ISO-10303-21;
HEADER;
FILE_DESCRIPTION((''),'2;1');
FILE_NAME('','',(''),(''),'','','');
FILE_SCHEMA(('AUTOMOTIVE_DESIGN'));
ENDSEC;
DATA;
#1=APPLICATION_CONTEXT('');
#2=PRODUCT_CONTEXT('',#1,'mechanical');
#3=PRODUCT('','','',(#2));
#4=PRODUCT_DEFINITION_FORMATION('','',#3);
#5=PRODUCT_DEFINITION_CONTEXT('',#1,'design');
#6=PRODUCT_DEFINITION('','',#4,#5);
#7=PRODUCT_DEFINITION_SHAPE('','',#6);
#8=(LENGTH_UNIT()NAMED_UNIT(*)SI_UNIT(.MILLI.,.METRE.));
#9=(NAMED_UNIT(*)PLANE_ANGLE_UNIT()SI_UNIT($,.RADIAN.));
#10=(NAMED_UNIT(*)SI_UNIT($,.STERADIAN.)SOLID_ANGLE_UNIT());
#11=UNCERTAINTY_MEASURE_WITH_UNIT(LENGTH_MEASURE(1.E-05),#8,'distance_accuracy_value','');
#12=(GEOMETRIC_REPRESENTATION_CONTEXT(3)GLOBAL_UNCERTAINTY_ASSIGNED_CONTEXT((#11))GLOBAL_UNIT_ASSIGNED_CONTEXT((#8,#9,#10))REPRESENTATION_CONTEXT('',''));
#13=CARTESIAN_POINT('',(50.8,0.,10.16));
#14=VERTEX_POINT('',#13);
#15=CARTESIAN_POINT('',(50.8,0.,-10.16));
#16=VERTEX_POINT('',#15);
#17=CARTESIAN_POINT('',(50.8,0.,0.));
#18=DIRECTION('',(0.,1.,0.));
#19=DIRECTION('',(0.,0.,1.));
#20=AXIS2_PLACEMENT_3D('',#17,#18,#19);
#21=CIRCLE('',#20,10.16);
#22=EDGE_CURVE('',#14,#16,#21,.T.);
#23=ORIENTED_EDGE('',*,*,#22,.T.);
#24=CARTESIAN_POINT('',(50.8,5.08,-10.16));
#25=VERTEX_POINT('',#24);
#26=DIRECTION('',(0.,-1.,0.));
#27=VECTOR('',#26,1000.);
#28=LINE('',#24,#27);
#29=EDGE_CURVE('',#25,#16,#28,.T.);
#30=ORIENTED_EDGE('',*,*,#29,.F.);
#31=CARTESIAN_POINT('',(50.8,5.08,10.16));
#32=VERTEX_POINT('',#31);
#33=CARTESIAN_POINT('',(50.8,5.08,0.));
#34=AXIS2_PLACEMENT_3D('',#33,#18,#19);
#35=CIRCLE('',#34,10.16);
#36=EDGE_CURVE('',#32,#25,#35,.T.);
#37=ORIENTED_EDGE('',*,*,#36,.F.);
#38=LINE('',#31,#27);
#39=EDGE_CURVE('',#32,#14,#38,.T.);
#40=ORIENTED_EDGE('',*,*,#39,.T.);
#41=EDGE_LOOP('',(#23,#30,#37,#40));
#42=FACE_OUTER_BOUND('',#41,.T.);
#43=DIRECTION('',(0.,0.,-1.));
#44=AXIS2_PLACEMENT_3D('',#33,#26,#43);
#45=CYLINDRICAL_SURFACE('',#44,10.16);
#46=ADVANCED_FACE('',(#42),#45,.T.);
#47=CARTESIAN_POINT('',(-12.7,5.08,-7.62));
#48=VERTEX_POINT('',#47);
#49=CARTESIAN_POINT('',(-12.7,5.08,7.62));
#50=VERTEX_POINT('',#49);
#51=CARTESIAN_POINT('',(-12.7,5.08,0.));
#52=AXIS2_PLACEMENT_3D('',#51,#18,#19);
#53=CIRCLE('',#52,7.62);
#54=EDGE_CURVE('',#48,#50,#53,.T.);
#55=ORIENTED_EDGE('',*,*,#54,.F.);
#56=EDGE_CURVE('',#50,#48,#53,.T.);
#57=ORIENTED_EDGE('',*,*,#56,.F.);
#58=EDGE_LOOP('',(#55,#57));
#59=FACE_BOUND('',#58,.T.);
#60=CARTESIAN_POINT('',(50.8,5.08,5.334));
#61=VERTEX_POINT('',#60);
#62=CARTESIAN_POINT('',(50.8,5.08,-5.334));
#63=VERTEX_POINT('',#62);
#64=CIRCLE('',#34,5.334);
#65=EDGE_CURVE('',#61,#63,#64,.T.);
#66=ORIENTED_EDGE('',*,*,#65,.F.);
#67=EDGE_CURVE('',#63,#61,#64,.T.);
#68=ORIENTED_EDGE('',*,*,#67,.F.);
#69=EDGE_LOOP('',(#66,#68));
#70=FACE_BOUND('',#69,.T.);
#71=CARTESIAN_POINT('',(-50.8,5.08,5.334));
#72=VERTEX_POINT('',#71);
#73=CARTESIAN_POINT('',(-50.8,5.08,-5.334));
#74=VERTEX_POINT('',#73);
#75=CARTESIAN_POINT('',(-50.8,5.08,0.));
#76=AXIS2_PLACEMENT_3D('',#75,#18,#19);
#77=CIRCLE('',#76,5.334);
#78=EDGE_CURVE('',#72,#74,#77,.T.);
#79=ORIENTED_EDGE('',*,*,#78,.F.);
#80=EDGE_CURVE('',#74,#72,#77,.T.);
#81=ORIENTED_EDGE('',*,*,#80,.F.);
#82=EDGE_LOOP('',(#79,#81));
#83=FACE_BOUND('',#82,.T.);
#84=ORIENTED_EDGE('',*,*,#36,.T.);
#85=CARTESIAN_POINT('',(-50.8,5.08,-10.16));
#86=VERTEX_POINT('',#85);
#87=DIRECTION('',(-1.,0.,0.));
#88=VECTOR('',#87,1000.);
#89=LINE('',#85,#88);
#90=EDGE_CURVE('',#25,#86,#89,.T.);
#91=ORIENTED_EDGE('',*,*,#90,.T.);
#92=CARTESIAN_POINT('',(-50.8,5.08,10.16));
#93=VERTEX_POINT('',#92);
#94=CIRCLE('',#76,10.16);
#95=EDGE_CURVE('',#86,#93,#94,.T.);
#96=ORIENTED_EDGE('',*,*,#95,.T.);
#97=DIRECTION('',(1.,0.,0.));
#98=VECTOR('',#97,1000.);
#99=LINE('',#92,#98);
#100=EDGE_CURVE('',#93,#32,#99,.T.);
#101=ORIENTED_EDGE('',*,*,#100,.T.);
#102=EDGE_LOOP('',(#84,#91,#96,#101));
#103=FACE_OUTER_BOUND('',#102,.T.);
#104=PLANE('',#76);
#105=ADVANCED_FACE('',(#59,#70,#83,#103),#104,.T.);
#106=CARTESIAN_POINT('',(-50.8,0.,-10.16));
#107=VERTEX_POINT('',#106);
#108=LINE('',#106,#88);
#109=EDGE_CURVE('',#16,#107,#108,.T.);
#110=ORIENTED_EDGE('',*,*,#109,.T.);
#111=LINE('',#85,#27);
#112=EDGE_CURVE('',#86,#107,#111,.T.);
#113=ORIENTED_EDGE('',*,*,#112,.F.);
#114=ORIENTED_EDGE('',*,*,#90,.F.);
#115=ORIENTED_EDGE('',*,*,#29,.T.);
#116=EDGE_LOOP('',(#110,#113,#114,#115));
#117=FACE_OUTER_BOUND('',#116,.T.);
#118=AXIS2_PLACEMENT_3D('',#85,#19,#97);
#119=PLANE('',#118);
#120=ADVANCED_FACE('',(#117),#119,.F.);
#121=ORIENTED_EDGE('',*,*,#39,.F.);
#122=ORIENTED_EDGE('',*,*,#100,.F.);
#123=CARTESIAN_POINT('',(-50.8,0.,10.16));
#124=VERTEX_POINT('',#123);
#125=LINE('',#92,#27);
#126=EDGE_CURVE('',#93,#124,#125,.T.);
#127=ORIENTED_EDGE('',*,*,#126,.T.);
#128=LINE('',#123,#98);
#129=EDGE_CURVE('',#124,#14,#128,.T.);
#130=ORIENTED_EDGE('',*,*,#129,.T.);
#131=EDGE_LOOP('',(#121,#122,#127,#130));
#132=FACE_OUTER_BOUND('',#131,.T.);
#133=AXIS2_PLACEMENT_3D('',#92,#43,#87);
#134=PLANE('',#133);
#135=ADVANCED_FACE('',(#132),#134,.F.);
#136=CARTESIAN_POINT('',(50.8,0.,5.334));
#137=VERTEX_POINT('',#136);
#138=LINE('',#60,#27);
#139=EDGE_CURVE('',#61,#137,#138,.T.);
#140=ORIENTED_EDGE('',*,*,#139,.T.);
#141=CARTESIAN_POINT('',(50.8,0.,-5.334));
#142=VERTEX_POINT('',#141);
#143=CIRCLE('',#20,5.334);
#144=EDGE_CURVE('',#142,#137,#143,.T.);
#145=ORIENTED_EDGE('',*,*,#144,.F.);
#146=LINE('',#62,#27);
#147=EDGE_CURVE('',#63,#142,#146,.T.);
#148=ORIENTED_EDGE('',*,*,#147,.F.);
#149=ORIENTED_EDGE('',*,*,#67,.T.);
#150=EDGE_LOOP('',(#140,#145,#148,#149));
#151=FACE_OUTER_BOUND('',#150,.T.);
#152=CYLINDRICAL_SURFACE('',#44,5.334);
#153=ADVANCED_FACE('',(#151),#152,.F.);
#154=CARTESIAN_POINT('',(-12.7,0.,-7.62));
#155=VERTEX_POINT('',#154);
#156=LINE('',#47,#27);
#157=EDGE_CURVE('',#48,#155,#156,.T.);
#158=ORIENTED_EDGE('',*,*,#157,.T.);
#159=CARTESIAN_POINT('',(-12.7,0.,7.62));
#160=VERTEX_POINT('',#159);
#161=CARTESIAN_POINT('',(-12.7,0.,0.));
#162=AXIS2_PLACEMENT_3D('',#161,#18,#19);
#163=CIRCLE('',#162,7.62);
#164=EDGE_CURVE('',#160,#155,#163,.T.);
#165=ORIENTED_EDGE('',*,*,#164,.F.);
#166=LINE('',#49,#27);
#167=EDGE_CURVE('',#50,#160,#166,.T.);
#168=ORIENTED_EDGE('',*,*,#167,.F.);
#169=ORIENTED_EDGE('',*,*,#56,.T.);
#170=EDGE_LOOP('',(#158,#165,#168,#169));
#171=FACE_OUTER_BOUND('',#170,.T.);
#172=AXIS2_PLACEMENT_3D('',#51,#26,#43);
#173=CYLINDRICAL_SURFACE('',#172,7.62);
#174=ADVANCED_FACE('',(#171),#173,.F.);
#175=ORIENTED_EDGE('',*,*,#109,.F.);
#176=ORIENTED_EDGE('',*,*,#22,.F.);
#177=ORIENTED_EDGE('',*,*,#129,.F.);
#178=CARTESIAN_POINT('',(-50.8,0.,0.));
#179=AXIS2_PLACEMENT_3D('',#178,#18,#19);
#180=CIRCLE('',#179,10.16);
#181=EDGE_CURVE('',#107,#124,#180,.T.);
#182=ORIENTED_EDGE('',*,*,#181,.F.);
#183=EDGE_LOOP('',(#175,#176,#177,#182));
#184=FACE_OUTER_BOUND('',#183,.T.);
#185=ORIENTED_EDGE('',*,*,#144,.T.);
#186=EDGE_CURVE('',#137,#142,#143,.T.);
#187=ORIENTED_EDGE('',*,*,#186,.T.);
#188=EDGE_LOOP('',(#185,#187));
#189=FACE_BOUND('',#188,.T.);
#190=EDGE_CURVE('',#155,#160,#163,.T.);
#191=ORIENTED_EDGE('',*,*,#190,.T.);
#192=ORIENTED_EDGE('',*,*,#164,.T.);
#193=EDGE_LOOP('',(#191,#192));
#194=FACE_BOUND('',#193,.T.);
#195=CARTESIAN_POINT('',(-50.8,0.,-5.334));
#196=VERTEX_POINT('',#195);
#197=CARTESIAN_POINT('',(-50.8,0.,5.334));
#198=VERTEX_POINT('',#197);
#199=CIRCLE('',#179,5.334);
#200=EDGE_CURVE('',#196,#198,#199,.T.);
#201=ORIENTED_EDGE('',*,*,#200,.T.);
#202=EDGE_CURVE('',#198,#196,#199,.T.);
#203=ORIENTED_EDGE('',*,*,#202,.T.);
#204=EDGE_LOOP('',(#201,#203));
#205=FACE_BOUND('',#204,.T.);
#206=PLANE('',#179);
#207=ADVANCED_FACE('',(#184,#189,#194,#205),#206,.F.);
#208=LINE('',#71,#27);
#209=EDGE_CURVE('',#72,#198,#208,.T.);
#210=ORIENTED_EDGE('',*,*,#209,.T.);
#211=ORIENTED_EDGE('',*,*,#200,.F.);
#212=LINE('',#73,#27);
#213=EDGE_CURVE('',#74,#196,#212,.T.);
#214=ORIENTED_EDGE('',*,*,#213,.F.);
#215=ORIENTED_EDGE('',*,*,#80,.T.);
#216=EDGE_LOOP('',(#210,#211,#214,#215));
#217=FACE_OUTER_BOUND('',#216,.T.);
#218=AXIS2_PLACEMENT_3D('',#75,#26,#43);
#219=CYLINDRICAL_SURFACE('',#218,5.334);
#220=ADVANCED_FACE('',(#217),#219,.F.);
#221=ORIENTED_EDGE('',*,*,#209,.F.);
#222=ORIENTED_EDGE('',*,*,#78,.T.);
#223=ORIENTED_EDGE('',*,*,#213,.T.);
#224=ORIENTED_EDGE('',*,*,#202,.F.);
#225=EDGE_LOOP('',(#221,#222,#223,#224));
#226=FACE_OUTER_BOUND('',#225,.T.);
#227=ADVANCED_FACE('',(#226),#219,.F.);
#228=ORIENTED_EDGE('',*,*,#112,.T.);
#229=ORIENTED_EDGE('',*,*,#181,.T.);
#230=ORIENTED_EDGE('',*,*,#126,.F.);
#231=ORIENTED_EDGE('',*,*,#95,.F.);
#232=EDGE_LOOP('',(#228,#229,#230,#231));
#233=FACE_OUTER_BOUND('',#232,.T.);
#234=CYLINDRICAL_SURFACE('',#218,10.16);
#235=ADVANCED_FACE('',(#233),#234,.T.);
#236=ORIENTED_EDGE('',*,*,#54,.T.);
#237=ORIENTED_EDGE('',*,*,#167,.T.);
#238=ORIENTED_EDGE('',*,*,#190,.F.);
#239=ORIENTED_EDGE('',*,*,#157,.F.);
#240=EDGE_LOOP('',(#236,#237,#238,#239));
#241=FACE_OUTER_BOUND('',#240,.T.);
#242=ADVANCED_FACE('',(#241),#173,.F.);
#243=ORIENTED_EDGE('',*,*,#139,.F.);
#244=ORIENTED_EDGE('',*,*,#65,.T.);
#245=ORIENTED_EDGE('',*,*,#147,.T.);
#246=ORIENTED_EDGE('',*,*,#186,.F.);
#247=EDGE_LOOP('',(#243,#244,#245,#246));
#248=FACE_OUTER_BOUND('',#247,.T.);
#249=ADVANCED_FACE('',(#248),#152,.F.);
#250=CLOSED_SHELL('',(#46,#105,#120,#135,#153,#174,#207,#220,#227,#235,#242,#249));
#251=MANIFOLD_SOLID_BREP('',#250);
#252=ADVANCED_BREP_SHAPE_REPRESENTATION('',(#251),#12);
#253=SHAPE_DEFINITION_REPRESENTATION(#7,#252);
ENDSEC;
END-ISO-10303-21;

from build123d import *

# Parameters (mm, degrees)
SKETCH1_R           = 2.667
SKETCH1_R_2         = 3.81
BOSS_EXTRUDE1_DEPTH = 2.54
SCALE1_SCALE        = 2


with BuildPart() as part:
    # Sketch1 → Boss-Extrude1 (new body)
    with BuildSketch(Plane(origin=(0, 0, 0), x_dir=(1, 0, 0), z_dir=(0, 1, 0))):
        with BuildLine():
            Line((-25.4, 5.08), (25.4, 5.08))
            ThreePointArc((25.4, 5.08), (30.48, 0), (25.4, -5.08))
            Line((25.4, -5.08), (-25.4, -5.08))
            ThreePointArc((-25.4, -5.08), (-30.48, 0), (-25.4, 5.08))
        make_face()
        with Locations(Location((-25.4, 0, 0), (0, 0, 270))):
            Circle(SKETCH1_R, mode=Mode.SUBTRACT)
        with Locations(Location((25.4, 0, 0), (0, 0, 270))):
            Circle(SKETCH1_R, mode=Mode.SUBTRACT)
        with Locations(Location((-6.35, 0, 0), (0, 0, 270))):
            Circle(SKETCH1_R_2, mode=Mode.SUBTRACT)
    extrude(amount=BOSS_EXTRUDE1_DEPTH)


with BuildPart() as part_1:
    # Scale1: scaled about (0, 0, 0)
    add(part.part.scale(SCALE1_SCALE))


solid = part_1.part
